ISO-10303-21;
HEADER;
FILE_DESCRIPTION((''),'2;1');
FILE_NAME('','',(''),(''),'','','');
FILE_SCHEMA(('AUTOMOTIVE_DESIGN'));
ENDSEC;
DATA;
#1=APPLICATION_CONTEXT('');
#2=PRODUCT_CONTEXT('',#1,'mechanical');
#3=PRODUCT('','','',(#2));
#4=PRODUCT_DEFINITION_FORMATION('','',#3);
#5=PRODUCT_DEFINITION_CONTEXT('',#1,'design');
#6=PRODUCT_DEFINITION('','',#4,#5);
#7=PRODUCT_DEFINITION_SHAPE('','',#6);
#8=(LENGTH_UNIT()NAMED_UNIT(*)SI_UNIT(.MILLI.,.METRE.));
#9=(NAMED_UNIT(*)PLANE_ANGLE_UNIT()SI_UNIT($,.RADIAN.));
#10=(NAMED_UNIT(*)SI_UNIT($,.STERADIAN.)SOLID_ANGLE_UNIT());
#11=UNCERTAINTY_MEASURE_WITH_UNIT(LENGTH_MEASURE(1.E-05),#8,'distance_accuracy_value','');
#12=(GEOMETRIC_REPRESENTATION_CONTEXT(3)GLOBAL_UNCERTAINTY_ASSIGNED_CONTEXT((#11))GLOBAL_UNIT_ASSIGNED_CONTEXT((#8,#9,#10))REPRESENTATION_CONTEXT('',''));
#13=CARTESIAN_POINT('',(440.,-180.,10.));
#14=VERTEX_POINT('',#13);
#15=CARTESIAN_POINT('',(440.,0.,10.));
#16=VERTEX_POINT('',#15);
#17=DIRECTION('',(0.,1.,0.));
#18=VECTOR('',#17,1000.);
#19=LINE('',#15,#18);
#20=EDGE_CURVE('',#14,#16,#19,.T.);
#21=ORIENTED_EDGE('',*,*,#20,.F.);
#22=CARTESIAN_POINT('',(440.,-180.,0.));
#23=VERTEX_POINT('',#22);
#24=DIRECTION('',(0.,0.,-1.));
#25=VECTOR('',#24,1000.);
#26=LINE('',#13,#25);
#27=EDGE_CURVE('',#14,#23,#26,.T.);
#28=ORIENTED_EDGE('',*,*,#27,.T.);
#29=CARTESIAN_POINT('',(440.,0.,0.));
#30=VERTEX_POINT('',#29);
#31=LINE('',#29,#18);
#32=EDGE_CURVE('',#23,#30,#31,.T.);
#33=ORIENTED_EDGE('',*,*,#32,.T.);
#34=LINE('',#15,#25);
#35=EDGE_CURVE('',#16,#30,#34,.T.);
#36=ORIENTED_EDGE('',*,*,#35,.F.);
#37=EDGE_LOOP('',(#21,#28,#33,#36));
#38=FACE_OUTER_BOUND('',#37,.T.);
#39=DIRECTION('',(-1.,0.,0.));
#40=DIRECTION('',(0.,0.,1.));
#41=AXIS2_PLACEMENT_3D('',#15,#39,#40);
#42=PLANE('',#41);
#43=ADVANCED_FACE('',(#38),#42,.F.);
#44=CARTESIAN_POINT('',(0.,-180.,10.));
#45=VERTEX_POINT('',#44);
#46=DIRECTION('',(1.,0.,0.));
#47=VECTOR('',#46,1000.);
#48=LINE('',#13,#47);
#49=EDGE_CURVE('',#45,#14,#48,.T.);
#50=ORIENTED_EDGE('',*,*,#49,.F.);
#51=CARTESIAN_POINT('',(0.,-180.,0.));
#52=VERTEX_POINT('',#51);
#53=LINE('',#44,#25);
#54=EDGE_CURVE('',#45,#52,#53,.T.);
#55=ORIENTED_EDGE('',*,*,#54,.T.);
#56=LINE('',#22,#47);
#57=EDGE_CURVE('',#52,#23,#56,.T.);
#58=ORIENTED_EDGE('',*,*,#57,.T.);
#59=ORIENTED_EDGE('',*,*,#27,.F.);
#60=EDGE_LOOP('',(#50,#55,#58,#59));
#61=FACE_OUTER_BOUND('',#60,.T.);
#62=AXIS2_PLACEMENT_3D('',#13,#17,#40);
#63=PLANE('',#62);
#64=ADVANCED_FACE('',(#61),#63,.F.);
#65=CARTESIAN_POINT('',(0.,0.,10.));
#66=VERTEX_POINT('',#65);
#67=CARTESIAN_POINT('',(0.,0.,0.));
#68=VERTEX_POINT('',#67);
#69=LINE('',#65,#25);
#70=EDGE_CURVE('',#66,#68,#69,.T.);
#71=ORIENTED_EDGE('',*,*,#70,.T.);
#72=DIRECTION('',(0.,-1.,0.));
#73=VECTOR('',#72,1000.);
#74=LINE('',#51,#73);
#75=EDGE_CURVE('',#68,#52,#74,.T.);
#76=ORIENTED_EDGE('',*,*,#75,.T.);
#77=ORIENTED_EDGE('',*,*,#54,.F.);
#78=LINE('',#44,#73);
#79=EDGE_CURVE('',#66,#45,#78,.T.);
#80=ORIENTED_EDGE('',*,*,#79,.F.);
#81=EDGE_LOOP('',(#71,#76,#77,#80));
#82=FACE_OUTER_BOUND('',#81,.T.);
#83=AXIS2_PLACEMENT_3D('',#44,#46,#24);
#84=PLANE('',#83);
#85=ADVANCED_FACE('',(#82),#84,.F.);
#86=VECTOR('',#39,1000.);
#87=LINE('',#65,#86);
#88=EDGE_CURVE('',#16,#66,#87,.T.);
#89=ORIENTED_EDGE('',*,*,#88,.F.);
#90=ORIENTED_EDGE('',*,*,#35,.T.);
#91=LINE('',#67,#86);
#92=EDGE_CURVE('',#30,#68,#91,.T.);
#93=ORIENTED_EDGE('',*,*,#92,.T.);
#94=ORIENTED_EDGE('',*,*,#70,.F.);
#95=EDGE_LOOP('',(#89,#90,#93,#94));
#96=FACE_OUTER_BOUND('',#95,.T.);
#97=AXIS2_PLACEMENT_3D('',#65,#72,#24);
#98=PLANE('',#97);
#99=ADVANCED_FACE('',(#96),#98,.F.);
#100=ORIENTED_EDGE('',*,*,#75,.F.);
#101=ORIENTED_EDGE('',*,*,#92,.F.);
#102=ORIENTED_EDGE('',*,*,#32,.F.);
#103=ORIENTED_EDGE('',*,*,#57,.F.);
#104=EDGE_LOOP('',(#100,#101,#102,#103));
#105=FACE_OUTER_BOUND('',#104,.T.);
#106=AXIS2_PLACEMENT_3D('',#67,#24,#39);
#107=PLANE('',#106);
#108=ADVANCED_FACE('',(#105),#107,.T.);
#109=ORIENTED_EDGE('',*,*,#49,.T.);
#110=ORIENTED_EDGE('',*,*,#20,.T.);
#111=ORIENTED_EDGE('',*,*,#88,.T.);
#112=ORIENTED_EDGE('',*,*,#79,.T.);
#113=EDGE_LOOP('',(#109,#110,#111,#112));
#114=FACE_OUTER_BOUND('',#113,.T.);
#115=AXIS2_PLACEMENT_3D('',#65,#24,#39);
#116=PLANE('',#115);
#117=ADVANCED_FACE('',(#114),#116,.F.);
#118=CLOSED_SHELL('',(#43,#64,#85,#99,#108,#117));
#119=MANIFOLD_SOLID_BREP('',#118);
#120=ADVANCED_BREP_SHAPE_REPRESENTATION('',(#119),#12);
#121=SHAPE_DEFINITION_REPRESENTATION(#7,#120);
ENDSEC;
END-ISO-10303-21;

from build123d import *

# Parameters (mm, degrees)
SKETCH_1_W      = 440
SKETCH_1_H      = 180
EXTRUDE_1_DEPTH = 10


with BuildPart() as part:
    # 草图1 → 凸台-拉伸1 (new body)
    with BuildSketch(Plane.XY):
        with Locations((220, -90)):
            Rectangle(SKETCH_1_W, SKETCH_1_H)
    extrude(amount=EXTRUDE_1_DEPTH)


solid = part.part
